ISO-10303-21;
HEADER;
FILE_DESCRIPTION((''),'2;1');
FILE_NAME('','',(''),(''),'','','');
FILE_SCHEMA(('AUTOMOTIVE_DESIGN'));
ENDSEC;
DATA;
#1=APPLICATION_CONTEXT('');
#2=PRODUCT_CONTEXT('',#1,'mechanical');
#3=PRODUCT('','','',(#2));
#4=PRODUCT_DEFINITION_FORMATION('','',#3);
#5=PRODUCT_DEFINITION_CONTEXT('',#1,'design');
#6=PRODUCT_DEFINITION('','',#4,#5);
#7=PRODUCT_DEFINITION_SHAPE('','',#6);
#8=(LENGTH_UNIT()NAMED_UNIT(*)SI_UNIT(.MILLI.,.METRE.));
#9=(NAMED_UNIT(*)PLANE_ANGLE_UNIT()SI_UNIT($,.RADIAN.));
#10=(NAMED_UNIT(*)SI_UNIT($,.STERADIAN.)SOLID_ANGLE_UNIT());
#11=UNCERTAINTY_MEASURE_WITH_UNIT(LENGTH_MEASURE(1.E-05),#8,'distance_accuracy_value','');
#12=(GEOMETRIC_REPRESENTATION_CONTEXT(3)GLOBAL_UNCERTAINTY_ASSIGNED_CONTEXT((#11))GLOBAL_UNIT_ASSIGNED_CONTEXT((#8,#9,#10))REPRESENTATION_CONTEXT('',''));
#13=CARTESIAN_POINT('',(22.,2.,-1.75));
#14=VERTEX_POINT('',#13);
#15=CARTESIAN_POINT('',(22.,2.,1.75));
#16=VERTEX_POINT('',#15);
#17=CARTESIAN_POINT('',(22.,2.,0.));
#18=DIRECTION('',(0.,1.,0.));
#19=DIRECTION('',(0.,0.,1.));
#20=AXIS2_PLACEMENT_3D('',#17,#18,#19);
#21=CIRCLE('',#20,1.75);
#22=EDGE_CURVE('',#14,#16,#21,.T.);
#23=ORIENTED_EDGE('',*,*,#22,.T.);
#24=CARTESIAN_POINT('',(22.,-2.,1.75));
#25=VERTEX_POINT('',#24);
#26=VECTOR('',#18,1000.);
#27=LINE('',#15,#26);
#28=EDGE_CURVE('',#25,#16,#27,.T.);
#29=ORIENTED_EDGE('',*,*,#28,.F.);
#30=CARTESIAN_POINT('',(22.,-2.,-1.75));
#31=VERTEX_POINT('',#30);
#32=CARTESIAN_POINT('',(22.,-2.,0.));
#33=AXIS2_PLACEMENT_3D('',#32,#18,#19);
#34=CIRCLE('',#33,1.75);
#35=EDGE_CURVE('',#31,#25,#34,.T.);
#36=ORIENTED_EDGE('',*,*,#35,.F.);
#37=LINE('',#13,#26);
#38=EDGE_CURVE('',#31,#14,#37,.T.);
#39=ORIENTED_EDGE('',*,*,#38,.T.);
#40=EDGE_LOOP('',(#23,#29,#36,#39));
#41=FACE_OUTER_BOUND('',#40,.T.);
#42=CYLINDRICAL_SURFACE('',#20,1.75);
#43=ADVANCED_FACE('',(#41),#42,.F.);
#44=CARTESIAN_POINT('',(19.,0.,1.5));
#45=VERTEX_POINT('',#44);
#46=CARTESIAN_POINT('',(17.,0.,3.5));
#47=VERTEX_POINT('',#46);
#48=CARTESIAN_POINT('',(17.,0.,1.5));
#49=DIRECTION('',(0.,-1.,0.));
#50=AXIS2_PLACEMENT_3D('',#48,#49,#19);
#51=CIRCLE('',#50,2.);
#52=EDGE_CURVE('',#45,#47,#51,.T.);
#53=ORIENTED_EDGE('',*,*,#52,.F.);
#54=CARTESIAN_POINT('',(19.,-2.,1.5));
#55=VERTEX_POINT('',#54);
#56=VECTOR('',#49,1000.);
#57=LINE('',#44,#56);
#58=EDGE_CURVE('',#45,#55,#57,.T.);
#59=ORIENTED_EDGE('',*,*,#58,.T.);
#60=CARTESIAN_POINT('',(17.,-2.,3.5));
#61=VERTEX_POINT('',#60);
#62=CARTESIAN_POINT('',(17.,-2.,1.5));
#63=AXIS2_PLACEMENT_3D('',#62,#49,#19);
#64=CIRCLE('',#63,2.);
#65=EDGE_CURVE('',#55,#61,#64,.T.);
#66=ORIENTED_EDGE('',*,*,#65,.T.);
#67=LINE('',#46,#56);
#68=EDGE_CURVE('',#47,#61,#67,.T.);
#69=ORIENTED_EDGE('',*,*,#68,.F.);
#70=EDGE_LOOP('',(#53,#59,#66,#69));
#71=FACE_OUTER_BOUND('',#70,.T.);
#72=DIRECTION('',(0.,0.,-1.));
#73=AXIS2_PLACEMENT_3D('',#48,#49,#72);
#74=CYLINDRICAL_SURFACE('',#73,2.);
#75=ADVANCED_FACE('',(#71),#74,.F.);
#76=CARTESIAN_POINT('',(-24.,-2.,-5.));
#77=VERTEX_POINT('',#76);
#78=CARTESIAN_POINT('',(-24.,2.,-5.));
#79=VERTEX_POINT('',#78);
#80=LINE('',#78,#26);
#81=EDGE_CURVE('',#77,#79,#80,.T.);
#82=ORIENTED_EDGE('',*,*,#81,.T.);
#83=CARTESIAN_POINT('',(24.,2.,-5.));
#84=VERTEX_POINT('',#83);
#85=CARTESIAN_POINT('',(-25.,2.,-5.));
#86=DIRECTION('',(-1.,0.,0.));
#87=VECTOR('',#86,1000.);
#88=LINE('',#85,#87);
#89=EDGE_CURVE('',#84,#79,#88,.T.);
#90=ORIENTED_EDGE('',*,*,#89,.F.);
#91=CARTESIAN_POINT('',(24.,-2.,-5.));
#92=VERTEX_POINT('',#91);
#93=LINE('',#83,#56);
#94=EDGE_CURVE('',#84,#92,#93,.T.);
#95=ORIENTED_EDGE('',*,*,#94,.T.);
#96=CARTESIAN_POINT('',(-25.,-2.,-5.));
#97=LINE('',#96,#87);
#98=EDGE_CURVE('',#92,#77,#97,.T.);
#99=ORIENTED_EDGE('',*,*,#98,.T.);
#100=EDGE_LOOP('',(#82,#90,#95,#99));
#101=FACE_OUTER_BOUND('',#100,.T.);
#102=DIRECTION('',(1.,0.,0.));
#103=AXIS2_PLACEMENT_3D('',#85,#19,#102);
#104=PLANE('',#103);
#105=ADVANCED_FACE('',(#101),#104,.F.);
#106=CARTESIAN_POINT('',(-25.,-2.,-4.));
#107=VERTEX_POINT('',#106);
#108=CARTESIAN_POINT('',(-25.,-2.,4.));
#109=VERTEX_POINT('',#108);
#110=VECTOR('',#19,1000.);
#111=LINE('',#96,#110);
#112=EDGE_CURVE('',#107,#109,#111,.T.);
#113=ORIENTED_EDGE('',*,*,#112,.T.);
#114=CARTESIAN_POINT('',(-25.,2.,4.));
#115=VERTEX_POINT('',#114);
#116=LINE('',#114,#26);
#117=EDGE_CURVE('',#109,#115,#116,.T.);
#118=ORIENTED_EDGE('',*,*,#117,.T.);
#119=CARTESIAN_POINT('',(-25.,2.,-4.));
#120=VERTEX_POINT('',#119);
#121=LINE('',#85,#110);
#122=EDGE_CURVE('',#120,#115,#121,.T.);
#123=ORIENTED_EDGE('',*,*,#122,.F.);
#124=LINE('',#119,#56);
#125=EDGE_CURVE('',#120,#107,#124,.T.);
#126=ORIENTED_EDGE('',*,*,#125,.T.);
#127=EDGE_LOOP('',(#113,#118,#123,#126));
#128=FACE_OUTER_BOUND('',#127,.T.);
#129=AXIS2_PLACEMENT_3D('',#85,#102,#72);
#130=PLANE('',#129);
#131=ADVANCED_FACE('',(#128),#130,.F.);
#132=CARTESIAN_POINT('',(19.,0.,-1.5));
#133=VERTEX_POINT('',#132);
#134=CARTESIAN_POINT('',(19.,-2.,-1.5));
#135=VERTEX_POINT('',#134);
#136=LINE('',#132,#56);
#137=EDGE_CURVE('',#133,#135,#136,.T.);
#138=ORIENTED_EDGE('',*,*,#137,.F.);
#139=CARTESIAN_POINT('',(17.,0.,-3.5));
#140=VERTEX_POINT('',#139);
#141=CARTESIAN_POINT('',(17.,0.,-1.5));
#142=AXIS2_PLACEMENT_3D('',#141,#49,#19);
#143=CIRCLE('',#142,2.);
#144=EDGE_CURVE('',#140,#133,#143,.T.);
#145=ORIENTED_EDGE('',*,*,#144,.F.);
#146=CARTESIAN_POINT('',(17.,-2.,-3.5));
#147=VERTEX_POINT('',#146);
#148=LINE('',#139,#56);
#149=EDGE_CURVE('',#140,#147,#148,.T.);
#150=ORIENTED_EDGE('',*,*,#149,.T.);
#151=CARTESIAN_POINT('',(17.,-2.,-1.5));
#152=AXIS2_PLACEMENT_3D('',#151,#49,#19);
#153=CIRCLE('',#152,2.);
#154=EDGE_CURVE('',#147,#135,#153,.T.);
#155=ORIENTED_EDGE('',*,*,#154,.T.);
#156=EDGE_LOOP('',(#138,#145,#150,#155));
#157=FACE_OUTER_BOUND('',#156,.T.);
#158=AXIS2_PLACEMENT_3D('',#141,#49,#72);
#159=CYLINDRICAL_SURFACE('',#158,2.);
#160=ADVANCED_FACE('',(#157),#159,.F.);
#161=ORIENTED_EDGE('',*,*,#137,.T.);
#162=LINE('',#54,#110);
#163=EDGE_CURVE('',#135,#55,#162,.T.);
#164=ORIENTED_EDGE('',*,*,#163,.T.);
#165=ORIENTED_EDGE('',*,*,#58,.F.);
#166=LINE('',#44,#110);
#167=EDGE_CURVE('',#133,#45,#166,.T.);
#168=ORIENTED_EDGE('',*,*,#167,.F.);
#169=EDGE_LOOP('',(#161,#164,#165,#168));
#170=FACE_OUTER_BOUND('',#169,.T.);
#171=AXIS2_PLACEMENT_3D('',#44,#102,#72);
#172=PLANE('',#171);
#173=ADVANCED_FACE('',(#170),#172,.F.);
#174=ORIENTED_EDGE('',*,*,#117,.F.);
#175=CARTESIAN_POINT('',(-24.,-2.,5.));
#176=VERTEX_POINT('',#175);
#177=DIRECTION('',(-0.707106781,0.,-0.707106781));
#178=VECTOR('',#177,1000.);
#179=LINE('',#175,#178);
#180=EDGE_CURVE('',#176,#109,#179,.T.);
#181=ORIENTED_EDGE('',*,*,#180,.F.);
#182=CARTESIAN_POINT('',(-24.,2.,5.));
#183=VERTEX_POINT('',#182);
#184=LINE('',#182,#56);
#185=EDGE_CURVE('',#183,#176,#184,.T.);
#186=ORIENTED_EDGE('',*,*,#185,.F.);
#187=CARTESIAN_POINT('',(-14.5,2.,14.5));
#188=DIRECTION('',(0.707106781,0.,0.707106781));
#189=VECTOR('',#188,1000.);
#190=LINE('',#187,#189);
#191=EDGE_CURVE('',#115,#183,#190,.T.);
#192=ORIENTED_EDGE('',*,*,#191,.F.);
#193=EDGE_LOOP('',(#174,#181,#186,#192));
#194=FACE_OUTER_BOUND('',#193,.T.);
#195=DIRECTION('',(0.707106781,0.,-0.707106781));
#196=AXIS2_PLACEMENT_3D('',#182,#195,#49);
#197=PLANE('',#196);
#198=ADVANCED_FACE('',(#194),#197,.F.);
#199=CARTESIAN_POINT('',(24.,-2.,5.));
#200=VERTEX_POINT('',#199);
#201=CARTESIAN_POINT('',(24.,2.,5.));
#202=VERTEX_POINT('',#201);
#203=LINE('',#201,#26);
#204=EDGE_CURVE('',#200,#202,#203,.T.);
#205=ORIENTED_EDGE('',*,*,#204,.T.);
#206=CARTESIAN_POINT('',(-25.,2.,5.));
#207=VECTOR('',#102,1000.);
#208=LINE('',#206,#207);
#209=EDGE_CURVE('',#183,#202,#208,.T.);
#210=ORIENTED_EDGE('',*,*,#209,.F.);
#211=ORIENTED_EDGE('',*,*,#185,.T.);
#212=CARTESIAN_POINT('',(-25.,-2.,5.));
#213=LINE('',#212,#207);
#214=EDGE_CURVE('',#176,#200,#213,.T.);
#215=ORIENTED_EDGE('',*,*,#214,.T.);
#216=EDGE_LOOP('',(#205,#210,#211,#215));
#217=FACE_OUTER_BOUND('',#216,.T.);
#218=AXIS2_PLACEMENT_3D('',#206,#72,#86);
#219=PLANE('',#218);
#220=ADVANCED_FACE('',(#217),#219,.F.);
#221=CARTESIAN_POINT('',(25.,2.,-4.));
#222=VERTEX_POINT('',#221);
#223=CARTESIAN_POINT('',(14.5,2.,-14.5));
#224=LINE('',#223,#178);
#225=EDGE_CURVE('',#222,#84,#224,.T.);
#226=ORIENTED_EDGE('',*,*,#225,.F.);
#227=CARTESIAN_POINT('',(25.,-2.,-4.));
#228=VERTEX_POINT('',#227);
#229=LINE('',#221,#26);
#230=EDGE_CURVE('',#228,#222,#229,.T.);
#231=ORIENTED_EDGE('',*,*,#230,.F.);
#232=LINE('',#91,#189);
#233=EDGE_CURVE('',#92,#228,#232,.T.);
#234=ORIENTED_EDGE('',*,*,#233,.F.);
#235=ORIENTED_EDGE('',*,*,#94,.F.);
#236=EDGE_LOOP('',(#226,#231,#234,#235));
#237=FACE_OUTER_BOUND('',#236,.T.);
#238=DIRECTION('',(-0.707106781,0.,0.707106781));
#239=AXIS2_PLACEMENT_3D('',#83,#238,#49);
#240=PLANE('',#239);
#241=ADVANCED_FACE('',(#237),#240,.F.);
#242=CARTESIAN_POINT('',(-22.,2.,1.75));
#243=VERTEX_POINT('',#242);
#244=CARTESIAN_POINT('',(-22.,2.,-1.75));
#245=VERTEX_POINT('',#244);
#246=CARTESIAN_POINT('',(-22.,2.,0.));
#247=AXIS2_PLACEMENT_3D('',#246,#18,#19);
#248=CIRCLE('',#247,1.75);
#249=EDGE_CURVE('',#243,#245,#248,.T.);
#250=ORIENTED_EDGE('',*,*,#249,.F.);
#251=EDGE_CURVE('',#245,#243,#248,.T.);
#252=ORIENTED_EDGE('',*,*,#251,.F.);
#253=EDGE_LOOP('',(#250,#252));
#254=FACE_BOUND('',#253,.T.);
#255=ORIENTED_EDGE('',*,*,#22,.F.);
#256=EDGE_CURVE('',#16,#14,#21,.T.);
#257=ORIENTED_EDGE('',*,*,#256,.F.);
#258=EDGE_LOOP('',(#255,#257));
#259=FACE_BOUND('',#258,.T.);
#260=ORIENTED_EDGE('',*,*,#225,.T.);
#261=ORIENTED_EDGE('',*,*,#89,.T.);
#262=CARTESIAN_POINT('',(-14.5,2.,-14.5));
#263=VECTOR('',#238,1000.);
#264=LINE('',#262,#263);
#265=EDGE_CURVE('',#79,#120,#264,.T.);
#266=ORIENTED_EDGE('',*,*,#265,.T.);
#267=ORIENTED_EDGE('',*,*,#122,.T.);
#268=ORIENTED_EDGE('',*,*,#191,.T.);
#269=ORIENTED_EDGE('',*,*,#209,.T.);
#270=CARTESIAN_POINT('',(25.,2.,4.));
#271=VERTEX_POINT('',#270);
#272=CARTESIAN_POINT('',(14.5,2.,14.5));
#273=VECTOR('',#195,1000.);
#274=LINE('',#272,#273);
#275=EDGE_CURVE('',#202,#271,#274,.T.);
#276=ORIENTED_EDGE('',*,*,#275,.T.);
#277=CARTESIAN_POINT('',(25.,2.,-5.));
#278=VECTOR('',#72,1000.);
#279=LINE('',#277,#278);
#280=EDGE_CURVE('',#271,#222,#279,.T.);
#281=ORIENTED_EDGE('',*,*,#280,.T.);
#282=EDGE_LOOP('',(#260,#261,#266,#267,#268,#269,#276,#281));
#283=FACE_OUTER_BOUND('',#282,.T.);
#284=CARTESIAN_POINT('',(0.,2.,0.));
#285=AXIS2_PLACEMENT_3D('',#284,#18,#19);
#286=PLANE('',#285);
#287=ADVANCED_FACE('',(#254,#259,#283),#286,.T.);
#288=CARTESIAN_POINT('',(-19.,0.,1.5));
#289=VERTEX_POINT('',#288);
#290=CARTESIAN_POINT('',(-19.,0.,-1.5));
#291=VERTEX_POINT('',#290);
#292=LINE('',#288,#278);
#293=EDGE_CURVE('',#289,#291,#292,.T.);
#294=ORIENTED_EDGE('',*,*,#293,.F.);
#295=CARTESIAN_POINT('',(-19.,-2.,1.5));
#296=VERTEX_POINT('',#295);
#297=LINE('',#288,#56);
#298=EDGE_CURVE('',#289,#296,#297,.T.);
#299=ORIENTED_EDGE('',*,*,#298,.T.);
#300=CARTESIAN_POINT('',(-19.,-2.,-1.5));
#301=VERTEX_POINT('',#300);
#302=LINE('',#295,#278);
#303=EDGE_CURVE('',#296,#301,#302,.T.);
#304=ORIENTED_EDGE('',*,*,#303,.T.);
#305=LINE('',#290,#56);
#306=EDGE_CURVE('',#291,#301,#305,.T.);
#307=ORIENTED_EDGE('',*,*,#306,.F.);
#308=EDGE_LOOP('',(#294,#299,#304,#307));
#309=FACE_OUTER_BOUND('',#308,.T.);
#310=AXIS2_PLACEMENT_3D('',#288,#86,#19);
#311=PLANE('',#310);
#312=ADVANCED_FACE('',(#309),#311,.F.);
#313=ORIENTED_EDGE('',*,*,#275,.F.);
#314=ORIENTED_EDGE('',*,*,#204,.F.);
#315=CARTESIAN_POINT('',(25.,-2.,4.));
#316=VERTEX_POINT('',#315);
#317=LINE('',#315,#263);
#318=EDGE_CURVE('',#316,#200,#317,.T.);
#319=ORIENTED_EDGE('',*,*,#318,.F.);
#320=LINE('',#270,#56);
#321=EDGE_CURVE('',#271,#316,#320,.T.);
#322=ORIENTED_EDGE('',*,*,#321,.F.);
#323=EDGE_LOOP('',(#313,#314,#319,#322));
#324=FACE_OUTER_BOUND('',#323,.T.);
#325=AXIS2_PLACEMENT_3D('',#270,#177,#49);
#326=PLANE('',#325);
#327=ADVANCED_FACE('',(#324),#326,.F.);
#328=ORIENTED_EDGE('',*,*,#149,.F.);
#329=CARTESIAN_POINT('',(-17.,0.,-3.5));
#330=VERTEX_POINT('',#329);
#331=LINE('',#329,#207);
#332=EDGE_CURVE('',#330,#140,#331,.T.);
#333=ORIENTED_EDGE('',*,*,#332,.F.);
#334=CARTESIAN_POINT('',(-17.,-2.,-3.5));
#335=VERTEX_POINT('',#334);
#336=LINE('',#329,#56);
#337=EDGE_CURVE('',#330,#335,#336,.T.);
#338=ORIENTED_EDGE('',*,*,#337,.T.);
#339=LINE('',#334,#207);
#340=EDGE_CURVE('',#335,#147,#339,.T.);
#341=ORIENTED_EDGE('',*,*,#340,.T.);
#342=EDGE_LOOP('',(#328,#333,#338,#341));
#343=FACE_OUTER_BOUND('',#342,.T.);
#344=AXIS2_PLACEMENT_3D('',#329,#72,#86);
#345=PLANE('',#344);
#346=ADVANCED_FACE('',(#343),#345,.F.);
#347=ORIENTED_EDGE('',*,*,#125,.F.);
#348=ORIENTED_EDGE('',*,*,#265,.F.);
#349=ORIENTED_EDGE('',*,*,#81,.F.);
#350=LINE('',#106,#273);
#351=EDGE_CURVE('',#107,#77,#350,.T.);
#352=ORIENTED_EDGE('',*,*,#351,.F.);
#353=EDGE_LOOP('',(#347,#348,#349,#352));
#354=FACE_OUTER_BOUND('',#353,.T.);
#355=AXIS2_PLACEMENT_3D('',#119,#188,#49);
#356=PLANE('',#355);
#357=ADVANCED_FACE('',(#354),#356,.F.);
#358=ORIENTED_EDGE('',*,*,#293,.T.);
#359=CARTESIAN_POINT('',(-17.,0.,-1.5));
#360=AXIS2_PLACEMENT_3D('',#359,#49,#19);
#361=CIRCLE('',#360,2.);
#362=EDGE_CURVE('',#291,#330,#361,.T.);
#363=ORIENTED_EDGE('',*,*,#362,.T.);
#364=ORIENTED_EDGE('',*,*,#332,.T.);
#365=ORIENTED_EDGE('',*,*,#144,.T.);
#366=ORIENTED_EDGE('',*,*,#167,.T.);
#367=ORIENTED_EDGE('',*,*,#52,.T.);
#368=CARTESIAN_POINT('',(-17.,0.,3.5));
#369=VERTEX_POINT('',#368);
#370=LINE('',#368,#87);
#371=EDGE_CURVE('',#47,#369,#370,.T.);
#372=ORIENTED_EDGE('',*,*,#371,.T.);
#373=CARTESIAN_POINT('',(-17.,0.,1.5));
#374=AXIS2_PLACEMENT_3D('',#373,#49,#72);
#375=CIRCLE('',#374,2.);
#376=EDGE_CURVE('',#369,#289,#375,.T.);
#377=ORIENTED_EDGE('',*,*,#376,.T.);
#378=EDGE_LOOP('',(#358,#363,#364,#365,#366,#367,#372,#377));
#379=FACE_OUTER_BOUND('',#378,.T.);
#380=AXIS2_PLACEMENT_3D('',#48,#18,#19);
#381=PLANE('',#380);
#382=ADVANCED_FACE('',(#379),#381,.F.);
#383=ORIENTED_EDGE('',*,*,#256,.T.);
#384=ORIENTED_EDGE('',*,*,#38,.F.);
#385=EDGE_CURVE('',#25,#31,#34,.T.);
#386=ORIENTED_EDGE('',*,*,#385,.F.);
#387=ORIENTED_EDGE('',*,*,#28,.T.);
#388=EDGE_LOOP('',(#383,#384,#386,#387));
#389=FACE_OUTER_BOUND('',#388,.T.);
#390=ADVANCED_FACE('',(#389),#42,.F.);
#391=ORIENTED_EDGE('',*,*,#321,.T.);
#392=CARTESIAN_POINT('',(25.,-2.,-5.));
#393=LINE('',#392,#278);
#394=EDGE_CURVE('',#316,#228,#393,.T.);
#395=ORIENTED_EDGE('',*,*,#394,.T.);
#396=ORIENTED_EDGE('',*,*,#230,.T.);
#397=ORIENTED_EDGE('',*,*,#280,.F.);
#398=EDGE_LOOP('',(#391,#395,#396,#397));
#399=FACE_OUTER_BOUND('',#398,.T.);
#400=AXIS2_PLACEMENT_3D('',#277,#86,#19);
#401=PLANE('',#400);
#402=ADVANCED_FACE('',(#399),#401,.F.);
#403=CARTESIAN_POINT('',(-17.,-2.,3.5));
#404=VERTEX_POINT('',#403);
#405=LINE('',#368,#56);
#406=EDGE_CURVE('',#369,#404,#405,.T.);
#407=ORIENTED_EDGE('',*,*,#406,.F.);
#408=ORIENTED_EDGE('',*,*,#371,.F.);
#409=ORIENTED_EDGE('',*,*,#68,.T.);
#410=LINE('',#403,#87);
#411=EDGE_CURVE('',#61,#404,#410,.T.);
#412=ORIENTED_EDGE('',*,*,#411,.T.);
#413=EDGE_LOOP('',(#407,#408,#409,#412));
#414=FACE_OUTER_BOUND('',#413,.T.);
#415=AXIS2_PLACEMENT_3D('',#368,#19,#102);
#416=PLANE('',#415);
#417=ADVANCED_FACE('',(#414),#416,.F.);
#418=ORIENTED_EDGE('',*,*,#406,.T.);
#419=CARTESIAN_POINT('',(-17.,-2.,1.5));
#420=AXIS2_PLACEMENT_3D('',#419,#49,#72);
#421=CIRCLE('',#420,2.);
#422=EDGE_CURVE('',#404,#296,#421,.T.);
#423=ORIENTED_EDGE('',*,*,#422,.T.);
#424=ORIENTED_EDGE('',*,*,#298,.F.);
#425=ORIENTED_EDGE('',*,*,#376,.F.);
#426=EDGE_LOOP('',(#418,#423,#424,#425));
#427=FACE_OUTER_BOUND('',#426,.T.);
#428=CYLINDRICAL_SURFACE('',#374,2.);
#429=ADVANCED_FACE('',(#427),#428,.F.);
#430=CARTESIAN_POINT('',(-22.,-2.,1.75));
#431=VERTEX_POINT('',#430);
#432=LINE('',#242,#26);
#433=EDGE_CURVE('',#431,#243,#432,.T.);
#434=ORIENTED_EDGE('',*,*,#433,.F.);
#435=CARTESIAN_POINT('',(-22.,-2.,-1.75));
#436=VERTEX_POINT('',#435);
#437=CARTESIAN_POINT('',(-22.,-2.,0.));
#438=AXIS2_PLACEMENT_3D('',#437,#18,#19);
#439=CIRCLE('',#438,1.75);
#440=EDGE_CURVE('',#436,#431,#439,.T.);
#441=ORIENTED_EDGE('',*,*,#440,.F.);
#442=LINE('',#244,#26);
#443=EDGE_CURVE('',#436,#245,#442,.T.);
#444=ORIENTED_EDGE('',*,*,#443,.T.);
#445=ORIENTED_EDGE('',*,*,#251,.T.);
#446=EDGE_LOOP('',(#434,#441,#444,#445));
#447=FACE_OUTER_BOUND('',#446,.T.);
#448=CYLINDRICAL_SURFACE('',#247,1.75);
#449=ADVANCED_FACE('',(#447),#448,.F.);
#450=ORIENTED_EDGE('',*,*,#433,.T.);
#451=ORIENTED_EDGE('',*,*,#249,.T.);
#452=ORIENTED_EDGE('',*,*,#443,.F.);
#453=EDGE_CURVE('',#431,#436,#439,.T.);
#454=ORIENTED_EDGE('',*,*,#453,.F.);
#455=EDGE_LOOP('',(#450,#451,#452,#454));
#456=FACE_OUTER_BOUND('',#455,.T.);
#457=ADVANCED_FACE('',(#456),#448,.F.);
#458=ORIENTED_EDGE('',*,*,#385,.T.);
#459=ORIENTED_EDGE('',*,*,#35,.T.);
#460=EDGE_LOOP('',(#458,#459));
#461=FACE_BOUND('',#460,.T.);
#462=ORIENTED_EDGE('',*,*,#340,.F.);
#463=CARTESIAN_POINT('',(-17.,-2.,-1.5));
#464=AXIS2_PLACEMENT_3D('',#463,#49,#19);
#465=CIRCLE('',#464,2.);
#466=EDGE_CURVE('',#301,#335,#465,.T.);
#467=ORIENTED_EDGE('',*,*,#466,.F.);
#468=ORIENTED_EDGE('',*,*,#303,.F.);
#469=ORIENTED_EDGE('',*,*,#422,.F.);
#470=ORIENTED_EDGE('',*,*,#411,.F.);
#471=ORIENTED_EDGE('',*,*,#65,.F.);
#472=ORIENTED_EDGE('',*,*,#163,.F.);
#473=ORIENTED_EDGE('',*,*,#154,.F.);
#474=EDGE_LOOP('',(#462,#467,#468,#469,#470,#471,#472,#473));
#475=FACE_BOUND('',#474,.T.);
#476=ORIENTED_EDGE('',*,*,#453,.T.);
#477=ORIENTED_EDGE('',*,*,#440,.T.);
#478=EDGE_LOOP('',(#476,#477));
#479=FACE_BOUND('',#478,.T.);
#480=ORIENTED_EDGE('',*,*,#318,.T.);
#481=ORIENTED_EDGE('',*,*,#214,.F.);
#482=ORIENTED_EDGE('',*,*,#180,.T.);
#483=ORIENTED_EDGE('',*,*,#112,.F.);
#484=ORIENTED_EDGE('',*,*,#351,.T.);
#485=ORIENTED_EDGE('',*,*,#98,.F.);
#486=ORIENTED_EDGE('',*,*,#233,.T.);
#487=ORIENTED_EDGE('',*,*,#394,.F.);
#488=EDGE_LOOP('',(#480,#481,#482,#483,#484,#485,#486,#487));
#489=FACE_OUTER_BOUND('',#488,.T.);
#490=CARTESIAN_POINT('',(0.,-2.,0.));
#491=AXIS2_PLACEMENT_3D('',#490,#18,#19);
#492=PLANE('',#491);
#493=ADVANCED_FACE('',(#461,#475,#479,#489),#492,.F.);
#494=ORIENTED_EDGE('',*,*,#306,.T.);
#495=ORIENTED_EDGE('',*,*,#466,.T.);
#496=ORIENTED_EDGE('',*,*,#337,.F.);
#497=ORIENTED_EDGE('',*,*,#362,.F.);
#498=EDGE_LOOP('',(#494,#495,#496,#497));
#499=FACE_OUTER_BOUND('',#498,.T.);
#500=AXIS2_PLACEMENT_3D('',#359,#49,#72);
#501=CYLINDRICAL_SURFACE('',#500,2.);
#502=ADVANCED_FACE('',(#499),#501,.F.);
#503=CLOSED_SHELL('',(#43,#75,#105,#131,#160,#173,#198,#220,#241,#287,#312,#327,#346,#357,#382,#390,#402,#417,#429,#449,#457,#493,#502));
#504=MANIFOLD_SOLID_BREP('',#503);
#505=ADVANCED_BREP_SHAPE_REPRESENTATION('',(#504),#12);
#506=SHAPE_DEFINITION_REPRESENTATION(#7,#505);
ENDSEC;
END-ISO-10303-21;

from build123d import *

# Parameters (mm, degrees)
SKETCH1_W                  = 50
SKETCH1_H                  = 10
BOSS_EXTRUDE1_DEPTH        = 2
F_3_5_3_5_DIAMETER_HOLE1_D = 3.5
CHAMFER1_SIZE              = 1
CUT_EXTRUDE1_DEPTH         = 2


with BuildPart() as part:
    # Sketch1 → Boss-Extrude1 (new, symmetric)
    with BuildSketch(Plane(origin=(0, 0, 0), x_dir=(1, 0, 0), z_dir=(0, 1, 0))):
        Rectangle(SKETCH1_W, SKETCH1_H)
    extrude(amount=BOSS_EXTRUDE1_DEPTH, both=True)

    # Ø3.5 (3.5) Diameter Hole1 (through all)
    with Locations(Plane(origin=(0, 2, 0), x_dir=(1, 0, 0), z_dir=(0, 1, 0))):
        with Locations((-22, 0), (22, 0)):
            Hole(F_3_5_3_5_DIAMETER_HOLE1_D / 2)

    # Chamfer1
    chamfer1_edges = [part.edges().sort_by_distance(p)[0] for p in [
        (25, 0, 5),
        (-25, 0, 5),
        (-25, 0, -5),
        (25, 0, -5),
    ]]
    chamfer(chamfer1_edges, length=CHAMFER1_SIZE)

    # Sketch4 → Cut-Extrude1 (cut)
    with BuildSketch(Plane.XZ.offset(2)):
        with BuildLine():
            Line((-17, 3.5), (17, 3.5))
            ThreePointArc((17, 3.5), (18.414213562, 2.914213562), (19, 1.5))
            Line((19, 1.5), (19, -1.5))
            ThreePointArc((19, -1.5), (18.414213562, -2.914213562), (17, -3.5))
            Line((17, -3.5), (-17, -3.5))
            ThreePointArc((-17, -3.5), (-18.414213562, -2.914213562), (-19, -1.5))
            Line((-19, -1.5), (-19, 1.5))
            ThreePointArc((-19, 1.5), (-18.414213562, 2.914213562), (-17, 3.5))
        make_face()
    extrude(amount=-CUT_EXTRUDE1_DEPTH, mode=Mode.SUBTRACT)


solid = part.part
